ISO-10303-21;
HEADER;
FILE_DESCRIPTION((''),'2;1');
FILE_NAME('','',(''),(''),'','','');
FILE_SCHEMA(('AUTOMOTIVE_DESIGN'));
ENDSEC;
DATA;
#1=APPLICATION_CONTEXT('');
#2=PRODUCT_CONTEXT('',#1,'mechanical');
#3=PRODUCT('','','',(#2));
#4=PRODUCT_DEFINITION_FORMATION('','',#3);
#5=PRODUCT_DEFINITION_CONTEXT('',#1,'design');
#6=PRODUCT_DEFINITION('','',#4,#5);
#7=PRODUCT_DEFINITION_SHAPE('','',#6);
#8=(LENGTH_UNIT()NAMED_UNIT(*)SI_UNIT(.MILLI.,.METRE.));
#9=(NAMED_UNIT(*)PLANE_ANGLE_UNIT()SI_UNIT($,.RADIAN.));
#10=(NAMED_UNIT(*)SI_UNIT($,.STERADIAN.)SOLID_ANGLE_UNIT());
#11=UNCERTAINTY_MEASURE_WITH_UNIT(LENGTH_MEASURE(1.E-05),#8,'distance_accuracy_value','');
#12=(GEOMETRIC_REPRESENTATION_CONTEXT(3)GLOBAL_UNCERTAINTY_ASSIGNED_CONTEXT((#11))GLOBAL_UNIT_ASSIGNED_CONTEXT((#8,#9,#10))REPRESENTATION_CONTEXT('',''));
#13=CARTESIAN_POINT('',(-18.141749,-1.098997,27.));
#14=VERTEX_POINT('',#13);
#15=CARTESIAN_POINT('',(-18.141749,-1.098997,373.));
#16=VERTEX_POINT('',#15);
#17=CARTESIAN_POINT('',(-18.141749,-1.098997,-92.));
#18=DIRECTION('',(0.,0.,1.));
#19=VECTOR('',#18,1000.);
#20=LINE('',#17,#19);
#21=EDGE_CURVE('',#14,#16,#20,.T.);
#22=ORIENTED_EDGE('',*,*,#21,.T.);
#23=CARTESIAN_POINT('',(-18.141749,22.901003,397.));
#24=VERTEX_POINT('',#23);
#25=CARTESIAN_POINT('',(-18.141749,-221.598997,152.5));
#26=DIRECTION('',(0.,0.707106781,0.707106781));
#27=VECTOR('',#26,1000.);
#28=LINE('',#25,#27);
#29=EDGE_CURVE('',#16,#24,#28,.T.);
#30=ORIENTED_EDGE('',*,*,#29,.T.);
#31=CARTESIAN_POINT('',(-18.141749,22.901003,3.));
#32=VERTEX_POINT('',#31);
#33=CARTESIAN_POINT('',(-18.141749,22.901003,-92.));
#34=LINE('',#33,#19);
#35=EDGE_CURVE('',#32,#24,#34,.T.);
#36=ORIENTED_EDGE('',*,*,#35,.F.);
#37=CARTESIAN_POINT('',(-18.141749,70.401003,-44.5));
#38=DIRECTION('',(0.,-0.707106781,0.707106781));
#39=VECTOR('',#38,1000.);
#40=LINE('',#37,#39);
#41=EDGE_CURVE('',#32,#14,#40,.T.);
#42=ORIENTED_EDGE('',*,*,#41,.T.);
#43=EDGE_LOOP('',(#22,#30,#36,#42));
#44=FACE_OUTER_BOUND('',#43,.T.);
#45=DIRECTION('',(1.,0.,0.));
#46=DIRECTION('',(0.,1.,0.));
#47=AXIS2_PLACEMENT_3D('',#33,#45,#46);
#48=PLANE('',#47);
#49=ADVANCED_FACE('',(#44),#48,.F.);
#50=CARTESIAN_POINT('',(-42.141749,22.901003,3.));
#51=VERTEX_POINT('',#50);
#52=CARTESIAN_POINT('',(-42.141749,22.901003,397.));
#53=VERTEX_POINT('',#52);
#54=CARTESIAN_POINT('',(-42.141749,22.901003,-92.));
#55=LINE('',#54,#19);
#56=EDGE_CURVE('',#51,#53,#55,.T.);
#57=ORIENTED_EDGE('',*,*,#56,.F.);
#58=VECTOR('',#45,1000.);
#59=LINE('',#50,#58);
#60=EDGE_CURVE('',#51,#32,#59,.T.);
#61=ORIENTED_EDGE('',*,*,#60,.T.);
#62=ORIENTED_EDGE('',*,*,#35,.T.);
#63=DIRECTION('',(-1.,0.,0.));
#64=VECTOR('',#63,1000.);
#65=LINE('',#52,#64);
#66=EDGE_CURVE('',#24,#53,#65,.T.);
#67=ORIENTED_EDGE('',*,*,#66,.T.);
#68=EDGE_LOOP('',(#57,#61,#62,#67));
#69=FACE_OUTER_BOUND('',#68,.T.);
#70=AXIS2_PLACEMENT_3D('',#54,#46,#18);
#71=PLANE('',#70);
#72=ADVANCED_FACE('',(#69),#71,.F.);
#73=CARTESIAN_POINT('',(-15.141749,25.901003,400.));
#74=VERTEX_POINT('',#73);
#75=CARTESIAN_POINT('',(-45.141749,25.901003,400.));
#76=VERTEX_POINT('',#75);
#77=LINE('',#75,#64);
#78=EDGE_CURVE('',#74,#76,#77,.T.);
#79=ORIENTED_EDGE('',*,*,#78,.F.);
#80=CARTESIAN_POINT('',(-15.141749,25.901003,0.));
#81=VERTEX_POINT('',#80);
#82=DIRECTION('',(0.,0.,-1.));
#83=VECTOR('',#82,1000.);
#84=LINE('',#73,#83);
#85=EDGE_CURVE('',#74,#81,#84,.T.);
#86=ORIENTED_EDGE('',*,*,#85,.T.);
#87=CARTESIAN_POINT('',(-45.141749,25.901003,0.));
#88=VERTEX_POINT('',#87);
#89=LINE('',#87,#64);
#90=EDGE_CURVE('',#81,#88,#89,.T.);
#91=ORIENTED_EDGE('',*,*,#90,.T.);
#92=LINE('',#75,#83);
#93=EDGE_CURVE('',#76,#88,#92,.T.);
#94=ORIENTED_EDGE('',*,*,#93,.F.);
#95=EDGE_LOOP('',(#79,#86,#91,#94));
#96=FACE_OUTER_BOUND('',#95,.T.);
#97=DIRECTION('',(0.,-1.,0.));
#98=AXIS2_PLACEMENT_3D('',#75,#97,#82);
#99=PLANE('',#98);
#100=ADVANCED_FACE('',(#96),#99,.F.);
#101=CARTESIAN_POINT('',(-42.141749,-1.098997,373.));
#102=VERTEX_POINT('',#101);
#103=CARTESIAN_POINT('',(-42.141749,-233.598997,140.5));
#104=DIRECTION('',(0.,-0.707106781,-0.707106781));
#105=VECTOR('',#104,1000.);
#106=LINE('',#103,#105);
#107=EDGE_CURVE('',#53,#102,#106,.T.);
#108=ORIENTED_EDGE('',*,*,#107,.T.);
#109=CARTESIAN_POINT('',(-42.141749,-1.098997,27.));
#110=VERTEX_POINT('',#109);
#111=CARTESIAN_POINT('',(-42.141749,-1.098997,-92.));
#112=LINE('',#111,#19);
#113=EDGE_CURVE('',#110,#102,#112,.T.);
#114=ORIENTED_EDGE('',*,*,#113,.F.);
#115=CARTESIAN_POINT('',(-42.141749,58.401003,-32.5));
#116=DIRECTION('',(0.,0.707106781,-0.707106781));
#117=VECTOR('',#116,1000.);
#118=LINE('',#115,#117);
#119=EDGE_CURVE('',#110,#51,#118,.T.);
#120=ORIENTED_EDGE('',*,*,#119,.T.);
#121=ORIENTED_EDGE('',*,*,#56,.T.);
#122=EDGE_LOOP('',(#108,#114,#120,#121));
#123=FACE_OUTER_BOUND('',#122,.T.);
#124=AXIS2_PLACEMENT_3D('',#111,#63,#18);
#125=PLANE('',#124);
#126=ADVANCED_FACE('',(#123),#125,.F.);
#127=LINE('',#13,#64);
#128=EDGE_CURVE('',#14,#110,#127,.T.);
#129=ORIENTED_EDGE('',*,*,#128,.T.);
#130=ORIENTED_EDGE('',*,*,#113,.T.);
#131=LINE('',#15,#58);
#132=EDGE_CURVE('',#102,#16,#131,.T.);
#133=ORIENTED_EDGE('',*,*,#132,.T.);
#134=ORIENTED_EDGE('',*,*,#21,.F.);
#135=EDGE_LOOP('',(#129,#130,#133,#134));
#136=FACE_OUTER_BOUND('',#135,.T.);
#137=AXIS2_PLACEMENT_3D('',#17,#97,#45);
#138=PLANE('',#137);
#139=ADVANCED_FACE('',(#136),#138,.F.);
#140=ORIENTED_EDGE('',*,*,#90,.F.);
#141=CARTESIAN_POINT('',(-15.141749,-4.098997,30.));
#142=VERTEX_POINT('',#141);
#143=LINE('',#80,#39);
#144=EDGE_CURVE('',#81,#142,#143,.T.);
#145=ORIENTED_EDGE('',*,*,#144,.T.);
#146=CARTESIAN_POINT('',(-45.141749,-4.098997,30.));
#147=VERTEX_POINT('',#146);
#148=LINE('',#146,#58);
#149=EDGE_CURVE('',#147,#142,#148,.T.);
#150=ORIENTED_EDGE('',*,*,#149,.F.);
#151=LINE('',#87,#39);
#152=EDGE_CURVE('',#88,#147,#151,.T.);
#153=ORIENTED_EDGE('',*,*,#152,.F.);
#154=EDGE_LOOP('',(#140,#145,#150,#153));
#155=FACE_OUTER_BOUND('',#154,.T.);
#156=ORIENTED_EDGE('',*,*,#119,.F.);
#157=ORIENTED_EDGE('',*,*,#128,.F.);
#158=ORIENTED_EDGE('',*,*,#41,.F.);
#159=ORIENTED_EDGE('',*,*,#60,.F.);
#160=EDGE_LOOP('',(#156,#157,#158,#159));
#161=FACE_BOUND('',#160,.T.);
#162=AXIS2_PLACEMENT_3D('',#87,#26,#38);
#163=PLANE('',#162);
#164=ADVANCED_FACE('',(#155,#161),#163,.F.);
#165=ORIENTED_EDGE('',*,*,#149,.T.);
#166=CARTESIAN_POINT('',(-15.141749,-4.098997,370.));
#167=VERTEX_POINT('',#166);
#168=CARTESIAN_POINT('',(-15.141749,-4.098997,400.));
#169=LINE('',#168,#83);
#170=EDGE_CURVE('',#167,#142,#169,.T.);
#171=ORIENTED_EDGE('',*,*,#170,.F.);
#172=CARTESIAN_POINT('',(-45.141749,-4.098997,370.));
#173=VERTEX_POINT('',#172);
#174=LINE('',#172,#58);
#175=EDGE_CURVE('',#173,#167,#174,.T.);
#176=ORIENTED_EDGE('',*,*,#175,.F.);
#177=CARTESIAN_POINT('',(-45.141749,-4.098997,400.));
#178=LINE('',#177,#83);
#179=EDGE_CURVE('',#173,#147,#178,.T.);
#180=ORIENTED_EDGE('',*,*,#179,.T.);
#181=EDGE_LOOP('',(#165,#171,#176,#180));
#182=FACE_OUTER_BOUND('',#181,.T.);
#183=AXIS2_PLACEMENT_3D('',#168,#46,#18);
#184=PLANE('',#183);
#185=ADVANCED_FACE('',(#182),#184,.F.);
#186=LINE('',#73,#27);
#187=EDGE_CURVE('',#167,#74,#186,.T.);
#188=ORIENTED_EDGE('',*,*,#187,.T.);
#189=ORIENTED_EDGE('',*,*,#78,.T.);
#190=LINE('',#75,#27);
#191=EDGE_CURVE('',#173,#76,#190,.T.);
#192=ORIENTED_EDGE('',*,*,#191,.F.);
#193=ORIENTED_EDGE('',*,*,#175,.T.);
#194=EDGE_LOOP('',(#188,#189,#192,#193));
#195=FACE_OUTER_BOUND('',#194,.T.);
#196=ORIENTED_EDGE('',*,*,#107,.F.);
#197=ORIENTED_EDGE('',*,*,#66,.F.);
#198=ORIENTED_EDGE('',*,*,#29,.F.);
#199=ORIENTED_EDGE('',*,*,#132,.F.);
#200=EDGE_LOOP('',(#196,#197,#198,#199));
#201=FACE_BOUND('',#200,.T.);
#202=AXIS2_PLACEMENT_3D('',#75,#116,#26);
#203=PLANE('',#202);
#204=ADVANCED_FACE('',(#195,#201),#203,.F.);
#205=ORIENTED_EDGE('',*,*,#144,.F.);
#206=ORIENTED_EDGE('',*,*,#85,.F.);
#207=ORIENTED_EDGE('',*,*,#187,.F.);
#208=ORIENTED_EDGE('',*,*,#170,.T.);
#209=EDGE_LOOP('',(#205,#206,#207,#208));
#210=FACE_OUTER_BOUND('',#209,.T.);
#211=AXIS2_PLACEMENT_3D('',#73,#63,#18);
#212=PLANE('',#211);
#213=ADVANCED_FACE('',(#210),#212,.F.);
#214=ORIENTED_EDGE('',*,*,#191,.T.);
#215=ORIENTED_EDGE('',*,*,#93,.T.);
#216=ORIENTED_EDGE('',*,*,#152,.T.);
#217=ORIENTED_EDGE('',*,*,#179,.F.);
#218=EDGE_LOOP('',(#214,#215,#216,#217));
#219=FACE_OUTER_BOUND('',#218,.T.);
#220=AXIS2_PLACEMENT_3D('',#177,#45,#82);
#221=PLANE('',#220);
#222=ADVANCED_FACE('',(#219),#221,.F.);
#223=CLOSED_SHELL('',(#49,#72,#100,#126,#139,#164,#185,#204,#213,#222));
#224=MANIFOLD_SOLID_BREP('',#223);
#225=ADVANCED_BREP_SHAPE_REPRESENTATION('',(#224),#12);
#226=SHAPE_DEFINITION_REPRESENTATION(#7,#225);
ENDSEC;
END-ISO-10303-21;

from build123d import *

# Parameters (mm, degrees)
SKETCH1_W           = 30
SKETCH1_H           = 30
BOSS_EXTRUDE1_DEPTH = 400
SKETCH2_W           = 24
SKETCH2_H           = 24
CUT_EXTRUDE1_DEPTH  = 492
CUT_EXTRUDE3_DEPTH  = 402.958781438
CUT_EXTRUDE6_DEPTH  = 402.958781438


with BuildPart() as part:
    # Sketch1 → Boss-Extrude1 (new body)
    with BuildSketch(Plane.XY):
        with Locations((-30.141748722, 10.901003365)):
            Rectangle(SKETCH1_W, SKETCH1_H)
    extrude(amount=BOSS_EXTRUDE1_DEPTH)

    # Sketch2 → Cut-Extrude1 (cut)
    with BuildSketch(Plane.XY.offset(400)):
        with Locations((-30.141748722, 10.901003365)):
            Rectangle(SKETCH2_W, SKETCH2_H)
    extrude(amount=-CUT_EXTRUDE1_DEPTH, mode=Mode.SUBTRACT)

    # Sketch4 → Cut-Extrude3 (cut, through all)
    with BuildSketch(Plane(origin=(-15.141748722, 0, 0), x_dir=(0, 0, -1), z_dir=(1, 0, 0))):
        Polygon((0, 25.901003365), (-30, -4.098996635), (0, -4.098996635), align=None)
    extrude(amount=-CUT_EXTRUDE3_DEPTH, mode=Mode.SUBTRACT)

    # Sketch8 → Cut-Extrude6 (cut, through all)
    with BuildSketch(Plane(origin=(-15.141748722, 0, 0), x_dir=(0, 0, -1), z_dir=(1, 0, 0))):
        Polygon((-400, 25.901003365), (-370, -4.098996635), (-400, -4.098996635), align=None)
    extrude(amount=-CUT_EXTRUDE6_DEPTH, mode=Mode.SUBTRACT)


solid = part.part
